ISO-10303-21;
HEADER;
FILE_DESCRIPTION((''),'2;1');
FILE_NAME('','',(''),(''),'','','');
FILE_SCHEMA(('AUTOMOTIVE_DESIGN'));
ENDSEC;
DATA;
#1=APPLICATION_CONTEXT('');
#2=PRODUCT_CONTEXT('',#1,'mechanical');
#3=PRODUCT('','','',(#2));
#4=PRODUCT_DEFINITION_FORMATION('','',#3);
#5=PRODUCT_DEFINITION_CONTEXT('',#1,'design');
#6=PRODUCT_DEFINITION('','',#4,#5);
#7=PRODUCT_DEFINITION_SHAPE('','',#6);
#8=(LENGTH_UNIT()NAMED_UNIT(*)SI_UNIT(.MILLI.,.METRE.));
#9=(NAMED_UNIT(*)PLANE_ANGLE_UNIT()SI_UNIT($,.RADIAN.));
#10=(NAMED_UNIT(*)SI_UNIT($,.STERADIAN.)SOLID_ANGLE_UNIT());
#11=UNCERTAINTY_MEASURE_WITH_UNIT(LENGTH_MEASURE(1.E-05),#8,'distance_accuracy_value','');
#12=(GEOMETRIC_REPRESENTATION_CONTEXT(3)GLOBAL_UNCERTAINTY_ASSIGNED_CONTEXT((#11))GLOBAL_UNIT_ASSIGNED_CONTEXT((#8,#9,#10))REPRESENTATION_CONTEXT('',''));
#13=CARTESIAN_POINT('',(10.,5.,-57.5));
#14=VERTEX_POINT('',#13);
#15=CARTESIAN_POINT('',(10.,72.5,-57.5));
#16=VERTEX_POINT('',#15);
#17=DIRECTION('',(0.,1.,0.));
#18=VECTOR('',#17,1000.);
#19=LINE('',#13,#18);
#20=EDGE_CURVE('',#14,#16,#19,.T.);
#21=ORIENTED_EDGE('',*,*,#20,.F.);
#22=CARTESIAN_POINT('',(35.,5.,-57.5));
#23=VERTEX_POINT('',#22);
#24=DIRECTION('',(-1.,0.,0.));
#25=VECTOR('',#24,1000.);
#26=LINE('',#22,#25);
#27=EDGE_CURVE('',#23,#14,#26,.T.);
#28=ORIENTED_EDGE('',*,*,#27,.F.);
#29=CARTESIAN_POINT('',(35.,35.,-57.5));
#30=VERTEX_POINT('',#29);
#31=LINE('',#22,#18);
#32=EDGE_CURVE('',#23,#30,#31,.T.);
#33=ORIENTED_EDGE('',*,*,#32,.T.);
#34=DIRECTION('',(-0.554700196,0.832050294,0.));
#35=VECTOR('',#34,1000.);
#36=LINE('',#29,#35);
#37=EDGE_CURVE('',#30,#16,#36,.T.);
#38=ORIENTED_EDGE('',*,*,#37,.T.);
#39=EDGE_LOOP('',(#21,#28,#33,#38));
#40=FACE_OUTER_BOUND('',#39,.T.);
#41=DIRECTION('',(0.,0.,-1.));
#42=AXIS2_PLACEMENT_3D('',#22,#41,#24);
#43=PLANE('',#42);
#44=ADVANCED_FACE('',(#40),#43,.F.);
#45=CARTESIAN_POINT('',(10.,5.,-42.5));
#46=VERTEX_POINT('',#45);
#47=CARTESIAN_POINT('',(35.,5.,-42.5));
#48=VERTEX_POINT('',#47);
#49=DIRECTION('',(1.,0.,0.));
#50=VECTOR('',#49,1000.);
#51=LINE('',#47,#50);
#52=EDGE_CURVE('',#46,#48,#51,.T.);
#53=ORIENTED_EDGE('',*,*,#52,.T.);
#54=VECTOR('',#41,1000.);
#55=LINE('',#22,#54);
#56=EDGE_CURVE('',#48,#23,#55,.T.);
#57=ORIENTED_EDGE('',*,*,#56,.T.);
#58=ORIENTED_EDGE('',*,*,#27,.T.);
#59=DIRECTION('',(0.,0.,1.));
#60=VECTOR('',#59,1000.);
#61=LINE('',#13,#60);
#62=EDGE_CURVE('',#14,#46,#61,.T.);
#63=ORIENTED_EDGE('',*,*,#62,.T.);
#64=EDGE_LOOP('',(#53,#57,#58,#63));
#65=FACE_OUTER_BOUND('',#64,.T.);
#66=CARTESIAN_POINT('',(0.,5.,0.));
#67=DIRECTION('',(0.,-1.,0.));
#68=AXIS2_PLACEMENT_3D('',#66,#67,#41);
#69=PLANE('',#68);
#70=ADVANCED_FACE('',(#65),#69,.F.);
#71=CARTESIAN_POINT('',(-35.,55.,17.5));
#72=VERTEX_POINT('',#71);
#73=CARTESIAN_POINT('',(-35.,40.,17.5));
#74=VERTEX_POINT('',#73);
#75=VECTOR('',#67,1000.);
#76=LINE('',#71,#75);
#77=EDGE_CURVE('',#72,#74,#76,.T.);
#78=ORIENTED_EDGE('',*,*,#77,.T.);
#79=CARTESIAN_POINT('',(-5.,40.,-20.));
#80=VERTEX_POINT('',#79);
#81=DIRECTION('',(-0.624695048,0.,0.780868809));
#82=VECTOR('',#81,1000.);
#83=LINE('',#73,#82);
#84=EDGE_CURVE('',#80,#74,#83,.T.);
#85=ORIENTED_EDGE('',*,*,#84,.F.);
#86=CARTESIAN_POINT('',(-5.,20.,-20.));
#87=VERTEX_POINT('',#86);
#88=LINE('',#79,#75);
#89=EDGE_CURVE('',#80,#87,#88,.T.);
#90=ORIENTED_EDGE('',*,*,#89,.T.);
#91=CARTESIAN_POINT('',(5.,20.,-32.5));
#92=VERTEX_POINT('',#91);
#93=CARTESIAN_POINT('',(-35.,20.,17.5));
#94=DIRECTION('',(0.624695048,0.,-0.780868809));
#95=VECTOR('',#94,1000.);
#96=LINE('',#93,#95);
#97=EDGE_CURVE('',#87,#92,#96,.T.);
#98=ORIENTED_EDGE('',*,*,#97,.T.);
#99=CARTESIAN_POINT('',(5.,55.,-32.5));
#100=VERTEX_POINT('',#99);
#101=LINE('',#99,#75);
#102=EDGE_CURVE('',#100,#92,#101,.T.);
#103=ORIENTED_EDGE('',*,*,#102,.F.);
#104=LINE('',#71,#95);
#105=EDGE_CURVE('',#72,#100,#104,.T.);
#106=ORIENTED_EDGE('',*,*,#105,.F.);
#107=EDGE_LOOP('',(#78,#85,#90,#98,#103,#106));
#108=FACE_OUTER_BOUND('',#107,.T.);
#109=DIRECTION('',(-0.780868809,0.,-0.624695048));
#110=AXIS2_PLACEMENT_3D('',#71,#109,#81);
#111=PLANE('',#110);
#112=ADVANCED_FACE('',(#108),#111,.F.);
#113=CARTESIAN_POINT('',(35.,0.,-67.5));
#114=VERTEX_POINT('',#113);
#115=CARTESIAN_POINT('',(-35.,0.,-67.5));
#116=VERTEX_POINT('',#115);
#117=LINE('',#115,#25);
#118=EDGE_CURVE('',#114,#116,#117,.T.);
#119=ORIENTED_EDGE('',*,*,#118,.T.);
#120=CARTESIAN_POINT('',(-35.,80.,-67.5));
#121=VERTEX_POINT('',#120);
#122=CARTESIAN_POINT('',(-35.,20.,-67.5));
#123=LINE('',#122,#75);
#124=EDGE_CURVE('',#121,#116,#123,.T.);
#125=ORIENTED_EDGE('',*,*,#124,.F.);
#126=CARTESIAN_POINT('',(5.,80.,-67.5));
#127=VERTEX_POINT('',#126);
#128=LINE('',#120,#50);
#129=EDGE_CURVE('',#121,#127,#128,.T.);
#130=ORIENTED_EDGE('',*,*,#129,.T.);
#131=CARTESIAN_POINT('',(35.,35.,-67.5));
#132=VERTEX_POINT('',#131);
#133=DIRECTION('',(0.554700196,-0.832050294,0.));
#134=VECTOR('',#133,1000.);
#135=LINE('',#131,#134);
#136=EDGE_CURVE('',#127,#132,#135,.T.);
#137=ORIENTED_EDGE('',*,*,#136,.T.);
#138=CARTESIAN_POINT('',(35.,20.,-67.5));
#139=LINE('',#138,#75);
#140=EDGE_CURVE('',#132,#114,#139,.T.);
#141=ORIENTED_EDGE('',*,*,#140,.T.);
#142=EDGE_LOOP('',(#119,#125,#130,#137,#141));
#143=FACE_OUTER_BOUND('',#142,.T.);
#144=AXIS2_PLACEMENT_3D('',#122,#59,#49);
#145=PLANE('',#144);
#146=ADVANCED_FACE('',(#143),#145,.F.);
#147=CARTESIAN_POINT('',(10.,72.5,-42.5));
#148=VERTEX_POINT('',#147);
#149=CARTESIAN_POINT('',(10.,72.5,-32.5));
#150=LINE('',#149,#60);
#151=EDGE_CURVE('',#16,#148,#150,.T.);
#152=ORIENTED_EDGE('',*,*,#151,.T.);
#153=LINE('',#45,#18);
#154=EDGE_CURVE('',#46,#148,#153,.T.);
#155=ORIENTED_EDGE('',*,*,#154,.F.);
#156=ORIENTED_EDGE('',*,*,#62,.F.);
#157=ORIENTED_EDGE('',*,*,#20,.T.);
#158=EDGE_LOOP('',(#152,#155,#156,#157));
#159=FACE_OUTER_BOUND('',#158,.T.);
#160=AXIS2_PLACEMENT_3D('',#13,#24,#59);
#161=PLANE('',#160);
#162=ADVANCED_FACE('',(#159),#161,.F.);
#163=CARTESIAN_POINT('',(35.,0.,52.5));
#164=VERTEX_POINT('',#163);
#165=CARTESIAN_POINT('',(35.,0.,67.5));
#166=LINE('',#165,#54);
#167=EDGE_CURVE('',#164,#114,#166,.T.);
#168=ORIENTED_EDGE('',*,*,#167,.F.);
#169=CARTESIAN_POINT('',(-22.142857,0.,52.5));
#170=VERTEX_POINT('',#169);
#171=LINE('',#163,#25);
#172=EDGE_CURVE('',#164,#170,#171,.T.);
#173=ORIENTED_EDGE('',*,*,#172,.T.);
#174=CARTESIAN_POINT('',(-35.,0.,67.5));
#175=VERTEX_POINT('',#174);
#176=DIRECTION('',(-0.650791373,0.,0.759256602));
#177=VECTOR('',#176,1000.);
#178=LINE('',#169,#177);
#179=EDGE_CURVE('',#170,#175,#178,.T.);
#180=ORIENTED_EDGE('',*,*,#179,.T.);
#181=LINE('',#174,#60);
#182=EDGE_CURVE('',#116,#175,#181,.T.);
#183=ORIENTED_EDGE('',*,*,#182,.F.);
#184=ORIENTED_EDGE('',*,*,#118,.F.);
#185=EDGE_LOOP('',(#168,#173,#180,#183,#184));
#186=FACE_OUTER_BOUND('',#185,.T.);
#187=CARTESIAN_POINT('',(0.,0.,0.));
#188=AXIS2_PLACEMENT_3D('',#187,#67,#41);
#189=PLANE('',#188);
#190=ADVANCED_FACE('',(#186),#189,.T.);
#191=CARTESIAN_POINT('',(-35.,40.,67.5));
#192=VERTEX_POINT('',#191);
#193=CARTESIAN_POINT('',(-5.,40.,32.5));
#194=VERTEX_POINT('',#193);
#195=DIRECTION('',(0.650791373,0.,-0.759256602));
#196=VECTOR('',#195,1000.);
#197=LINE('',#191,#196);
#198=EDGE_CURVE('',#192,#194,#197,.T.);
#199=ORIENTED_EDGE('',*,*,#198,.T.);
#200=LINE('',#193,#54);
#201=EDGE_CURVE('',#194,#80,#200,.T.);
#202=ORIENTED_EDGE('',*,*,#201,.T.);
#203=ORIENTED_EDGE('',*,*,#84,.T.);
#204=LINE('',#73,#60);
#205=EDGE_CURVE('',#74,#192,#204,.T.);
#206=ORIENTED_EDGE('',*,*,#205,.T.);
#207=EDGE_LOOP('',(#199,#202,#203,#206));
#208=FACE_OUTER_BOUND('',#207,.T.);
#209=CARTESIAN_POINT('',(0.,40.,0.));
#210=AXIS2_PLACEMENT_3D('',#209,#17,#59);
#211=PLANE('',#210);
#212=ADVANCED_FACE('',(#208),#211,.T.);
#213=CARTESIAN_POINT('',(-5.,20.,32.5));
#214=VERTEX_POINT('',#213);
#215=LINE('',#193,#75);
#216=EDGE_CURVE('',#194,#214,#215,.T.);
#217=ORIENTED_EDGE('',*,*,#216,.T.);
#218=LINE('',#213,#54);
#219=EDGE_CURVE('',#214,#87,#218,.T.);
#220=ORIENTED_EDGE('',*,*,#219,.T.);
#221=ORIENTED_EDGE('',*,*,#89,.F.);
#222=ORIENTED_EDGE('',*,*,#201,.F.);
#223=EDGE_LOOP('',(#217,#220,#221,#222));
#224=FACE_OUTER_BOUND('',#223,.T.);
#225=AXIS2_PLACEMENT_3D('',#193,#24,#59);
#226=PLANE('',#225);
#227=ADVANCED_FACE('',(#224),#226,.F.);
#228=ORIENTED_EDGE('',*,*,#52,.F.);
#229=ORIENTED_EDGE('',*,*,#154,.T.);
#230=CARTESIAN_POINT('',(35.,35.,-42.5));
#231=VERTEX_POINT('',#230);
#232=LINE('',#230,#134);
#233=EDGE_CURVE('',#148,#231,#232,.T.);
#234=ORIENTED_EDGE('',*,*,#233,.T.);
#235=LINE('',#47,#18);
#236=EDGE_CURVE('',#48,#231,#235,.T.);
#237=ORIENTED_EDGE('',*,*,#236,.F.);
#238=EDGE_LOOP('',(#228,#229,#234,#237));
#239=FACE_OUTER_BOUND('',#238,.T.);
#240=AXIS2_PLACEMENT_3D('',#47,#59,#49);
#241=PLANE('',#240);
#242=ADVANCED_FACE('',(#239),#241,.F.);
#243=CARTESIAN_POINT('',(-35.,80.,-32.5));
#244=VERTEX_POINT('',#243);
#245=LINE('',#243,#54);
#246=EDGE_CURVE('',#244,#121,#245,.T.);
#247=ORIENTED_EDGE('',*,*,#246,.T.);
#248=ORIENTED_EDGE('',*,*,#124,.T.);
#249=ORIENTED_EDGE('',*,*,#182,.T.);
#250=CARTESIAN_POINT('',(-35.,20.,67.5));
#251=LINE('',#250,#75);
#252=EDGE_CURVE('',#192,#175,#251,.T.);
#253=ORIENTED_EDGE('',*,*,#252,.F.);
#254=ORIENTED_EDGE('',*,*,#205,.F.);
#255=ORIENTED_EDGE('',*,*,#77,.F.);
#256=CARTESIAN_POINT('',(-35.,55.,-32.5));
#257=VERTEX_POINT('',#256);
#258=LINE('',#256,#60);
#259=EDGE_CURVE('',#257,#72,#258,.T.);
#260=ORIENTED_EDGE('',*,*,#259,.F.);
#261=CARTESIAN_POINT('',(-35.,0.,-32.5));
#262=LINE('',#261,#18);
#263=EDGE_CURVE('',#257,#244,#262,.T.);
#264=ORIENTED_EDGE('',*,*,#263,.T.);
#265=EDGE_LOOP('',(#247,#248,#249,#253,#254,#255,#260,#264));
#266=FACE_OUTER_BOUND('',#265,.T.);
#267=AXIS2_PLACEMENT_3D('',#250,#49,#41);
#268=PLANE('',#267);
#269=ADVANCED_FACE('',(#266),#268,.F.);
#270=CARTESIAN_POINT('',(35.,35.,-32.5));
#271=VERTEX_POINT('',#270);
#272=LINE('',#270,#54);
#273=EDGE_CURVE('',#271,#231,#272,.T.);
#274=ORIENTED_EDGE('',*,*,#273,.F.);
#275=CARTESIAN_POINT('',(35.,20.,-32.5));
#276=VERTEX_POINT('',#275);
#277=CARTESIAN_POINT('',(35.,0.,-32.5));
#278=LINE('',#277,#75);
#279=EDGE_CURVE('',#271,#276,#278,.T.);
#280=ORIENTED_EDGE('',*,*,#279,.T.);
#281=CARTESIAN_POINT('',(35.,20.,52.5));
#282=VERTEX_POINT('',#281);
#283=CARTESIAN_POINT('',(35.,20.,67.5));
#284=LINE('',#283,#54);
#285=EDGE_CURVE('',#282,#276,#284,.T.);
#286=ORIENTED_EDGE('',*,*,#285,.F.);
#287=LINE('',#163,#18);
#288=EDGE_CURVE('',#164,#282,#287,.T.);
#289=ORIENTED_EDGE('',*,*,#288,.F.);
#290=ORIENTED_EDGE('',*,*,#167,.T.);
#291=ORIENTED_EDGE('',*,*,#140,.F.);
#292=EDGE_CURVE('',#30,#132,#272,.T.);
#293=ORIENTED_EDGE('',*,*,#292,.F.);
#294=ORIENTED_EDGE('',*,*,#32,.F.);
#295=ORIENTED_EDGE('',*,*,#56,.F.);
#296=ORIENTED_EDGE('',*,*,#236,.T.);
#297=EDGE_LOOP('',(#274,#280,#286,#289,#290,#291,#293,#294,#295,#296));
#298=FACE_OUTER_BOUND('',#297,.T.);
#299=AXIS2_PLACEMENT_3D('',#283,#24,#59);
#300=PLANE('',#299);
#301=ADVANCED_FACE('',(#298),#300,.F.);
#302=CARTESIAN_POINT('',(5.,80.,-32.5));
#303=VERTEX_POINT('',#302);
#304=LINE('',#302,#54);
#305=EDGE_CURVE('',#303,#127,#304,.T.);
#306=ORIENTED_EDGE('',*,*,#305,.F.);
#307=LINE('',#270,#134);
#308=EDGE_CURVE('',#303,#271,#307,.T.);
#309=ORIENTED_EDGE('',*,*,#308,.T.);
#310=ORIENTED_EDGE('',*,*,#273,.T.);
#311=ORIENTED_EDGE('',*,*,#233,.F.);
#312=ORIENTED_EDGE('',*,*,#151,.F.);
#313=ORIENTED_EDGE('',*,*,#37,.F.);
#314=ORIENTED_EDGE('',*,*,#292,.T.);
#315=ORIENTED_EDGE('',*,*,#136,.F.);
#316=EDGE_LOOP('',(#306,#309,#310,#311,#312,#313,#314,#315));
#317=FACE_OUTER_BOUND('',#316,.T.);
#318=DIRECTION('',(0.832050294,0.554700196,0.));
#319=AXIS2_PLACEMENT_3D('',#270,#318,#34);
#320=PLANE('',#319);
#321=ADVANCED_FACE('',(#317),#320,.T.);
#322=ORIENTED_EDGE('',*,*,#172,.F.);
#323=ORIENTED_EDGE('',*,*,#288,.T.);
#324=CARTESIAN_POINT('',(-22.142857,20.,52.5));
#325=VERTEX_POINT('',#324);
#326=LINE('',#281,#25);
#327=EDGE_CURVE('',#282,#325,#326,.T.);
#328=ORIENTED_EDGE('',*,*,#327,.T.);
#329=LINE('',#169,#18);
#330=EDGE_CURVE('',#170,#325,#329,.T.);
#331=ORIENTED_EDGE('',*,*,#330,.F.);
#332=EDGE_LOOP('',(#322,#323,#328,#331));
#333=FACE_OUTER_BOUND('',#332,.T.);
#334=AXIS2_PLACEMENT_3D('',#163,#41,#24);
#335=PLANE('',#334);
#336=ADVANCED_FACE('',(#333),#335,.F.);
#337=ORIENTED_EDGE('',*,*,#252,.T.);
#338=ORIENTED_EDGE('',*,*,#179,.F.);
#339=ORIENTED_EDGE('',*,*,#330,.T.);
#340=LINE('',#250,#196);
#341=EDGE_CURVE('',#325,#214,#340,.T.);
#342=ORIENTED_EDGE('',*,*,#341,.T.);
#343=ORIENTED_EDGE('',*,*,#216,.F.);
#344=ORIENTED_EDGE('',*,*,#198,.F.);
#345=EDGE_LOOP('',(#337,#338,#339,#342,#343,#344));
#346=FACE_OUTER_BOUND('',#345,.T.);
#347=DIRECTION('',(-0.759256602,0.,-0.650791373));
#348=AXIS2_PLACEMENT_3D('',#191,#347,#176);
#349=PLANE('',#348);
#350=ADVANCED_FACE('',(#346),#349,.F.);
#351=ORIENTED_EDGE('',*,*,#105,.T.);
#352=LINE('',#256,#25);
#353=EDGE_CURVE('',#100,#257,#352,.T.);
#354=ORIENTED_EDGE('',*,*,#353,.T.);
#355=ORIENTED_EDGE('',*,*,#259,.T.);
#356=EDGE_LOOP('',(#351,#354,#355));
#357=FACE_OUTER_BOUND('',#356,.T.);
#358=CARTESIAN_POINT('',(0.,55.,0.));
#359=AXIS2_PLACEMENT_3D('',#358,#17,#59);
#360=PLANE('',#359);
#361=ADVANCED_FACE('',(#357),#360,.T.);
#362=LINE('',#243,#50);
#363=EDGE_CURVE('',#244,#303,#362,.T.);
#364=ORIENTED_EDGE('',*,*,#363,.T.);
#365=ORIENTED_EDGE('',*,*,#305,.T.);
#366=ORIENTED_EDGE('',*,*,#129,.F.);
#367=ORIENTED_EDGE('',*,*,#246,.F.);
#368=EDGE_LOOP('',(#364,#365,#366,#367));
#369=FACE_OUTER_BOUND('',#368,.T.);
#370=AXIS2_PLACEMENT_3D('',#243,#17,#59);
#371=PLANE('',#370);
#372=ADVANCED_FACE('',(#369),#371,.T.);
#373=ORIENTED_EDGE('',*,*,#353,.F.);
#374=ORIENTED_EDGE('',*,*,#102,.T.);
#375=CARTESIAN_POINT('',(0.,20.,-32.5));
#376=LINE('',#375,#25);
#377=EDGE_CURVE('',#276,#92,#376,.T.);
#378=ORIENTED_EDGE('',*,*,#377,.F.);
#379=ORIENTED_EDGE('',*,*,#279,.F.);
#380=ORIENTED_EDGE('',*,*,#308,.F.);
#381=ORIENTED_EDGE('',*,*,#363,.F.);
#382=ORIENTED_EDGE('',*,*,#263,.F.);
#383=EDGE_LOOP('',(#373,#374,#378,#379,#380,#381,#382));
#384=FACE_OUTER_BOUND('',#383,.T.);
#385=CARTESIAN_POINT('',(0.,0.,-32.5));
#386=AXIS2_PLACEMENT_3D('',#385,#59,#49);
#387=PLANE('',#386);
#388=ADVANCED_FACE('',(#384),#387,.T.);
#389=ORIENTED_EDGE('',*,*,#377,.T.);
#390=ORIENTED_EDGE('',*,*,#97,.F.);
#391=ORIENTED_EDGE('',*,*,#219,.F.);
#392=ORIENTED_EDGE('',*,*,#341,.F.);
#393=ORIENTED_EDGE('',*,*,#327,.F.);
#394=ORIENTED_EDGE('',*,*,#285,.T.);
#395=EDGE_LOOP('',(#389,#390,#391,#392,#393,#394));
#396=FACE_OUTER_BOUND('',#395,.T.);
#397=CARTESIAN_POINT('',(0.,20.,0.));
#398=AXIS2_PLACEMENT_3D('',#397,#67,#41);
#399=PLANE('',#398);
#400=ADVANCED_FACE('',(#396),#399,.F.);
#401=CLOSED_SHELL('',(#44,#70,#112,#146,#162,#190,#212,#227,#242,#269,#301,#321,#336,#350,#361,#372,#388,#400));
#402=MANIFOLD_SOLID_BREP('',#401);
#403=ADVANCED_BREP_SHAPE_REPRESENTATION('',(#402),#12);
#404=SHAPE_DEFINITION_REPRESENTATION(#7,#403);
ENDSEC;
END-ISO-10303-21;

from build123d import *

# Parameters (mm, degrees)
BASE_PLATE_SKETCH_W   = 70
BASE_PLATE_SKETCH_H   = 135
BASE_PLATE_DEPTH      = 20
TOWER_DEPTH           = 35
TOWER_WINDOW_SKETCH_W = 25
TOWER_WINDOW_SKETCH_H = 15
TOWER_WINDOW_DEPTH    = 75
UPPER_STEP_DEPTH      = 35
LOWER_STEP_DEPTH      = 20
STEP_NOTCH_DEPTH      = 20


with BuildPart() as part:
    # Base Plate Sketch → Base Plate (new body)
    with BuildSketch(Plane(origin=(0, 0, 0), x_dir=(1, 0, 0), z_dir=(0, 1, 0))):
        Rectangle(BASE_PLATE_SKETCH_W, BASE_PLATE_SKETCH_H)
    extrude(amount=BASE_PLATE_DEPTH)

    # Tower Profile Sketch → Tower (add)
    with BuildSketch(Plane(origin=(0, 0, -67.5), x_dir=(-1, 0, 0), z_dir=(0, 0, -1))):
        Polygon((35, 0), (35, 80), (-5, 80), (-35, 35), (-35, 0), align=None)
    extrude(amount=-TOWER_DEPTH)

    # Tower Window Sketch → Tower Window (cut)
    with BuildSketch(Plane(origin=(0, 80, 0), x_dir=(1, 0, 0), z_dir=(0, 1, 0))):
        with Locations((22.5, 50)):
            Rectangle(TOWER_WINDOW_SKETCH_W, TOWER_WINDOW_SKETCH_H)
    extrude(amount=-TOWER_WINDOW_DEPTH, mode=Mode.SUBTRACT)

    # Upper Step Sketch → Upper Step (add)
    with BuildSketch(Plane(origin=(0, 20, 0), x_dir=(1, 0, 0), z_dir=(0, 1, 0))):
        Polygon((-35, 32.5), (5, 32.5), (-35, -17.5), align=None)
    extrude(amount=UPPER_STEP_DEPTH)

    # Lower Step Sketch → Lower Step (add)
    with BuildSketch(Plane(origin=(0, 20, 0), x_dir=(1, 0, 0), z_dir=(0, 1, 0))):
        Polygon((-35, -17.5), (-35, -67.5), (-5, -32.5), (-5, 20), align=None)
    extrude(amount=LOWER_STEP_DEPTH)

    # Step Notch Sketch → Step Notch (cut)
    with BuildSketch(Plane(origin=(0, 20, 0), x_dir=(1, 0, 0), z_dir=(0, 1, 0))):
        Polygon((35, -67.5), (35, -52.5), (-22.142857143, -52.5), (-35, -67.5), align=None)
    extrude(amount=-STEP_NOTCH_DEPTH, mode=Mode.SUBTRACT)


solid = part.part
